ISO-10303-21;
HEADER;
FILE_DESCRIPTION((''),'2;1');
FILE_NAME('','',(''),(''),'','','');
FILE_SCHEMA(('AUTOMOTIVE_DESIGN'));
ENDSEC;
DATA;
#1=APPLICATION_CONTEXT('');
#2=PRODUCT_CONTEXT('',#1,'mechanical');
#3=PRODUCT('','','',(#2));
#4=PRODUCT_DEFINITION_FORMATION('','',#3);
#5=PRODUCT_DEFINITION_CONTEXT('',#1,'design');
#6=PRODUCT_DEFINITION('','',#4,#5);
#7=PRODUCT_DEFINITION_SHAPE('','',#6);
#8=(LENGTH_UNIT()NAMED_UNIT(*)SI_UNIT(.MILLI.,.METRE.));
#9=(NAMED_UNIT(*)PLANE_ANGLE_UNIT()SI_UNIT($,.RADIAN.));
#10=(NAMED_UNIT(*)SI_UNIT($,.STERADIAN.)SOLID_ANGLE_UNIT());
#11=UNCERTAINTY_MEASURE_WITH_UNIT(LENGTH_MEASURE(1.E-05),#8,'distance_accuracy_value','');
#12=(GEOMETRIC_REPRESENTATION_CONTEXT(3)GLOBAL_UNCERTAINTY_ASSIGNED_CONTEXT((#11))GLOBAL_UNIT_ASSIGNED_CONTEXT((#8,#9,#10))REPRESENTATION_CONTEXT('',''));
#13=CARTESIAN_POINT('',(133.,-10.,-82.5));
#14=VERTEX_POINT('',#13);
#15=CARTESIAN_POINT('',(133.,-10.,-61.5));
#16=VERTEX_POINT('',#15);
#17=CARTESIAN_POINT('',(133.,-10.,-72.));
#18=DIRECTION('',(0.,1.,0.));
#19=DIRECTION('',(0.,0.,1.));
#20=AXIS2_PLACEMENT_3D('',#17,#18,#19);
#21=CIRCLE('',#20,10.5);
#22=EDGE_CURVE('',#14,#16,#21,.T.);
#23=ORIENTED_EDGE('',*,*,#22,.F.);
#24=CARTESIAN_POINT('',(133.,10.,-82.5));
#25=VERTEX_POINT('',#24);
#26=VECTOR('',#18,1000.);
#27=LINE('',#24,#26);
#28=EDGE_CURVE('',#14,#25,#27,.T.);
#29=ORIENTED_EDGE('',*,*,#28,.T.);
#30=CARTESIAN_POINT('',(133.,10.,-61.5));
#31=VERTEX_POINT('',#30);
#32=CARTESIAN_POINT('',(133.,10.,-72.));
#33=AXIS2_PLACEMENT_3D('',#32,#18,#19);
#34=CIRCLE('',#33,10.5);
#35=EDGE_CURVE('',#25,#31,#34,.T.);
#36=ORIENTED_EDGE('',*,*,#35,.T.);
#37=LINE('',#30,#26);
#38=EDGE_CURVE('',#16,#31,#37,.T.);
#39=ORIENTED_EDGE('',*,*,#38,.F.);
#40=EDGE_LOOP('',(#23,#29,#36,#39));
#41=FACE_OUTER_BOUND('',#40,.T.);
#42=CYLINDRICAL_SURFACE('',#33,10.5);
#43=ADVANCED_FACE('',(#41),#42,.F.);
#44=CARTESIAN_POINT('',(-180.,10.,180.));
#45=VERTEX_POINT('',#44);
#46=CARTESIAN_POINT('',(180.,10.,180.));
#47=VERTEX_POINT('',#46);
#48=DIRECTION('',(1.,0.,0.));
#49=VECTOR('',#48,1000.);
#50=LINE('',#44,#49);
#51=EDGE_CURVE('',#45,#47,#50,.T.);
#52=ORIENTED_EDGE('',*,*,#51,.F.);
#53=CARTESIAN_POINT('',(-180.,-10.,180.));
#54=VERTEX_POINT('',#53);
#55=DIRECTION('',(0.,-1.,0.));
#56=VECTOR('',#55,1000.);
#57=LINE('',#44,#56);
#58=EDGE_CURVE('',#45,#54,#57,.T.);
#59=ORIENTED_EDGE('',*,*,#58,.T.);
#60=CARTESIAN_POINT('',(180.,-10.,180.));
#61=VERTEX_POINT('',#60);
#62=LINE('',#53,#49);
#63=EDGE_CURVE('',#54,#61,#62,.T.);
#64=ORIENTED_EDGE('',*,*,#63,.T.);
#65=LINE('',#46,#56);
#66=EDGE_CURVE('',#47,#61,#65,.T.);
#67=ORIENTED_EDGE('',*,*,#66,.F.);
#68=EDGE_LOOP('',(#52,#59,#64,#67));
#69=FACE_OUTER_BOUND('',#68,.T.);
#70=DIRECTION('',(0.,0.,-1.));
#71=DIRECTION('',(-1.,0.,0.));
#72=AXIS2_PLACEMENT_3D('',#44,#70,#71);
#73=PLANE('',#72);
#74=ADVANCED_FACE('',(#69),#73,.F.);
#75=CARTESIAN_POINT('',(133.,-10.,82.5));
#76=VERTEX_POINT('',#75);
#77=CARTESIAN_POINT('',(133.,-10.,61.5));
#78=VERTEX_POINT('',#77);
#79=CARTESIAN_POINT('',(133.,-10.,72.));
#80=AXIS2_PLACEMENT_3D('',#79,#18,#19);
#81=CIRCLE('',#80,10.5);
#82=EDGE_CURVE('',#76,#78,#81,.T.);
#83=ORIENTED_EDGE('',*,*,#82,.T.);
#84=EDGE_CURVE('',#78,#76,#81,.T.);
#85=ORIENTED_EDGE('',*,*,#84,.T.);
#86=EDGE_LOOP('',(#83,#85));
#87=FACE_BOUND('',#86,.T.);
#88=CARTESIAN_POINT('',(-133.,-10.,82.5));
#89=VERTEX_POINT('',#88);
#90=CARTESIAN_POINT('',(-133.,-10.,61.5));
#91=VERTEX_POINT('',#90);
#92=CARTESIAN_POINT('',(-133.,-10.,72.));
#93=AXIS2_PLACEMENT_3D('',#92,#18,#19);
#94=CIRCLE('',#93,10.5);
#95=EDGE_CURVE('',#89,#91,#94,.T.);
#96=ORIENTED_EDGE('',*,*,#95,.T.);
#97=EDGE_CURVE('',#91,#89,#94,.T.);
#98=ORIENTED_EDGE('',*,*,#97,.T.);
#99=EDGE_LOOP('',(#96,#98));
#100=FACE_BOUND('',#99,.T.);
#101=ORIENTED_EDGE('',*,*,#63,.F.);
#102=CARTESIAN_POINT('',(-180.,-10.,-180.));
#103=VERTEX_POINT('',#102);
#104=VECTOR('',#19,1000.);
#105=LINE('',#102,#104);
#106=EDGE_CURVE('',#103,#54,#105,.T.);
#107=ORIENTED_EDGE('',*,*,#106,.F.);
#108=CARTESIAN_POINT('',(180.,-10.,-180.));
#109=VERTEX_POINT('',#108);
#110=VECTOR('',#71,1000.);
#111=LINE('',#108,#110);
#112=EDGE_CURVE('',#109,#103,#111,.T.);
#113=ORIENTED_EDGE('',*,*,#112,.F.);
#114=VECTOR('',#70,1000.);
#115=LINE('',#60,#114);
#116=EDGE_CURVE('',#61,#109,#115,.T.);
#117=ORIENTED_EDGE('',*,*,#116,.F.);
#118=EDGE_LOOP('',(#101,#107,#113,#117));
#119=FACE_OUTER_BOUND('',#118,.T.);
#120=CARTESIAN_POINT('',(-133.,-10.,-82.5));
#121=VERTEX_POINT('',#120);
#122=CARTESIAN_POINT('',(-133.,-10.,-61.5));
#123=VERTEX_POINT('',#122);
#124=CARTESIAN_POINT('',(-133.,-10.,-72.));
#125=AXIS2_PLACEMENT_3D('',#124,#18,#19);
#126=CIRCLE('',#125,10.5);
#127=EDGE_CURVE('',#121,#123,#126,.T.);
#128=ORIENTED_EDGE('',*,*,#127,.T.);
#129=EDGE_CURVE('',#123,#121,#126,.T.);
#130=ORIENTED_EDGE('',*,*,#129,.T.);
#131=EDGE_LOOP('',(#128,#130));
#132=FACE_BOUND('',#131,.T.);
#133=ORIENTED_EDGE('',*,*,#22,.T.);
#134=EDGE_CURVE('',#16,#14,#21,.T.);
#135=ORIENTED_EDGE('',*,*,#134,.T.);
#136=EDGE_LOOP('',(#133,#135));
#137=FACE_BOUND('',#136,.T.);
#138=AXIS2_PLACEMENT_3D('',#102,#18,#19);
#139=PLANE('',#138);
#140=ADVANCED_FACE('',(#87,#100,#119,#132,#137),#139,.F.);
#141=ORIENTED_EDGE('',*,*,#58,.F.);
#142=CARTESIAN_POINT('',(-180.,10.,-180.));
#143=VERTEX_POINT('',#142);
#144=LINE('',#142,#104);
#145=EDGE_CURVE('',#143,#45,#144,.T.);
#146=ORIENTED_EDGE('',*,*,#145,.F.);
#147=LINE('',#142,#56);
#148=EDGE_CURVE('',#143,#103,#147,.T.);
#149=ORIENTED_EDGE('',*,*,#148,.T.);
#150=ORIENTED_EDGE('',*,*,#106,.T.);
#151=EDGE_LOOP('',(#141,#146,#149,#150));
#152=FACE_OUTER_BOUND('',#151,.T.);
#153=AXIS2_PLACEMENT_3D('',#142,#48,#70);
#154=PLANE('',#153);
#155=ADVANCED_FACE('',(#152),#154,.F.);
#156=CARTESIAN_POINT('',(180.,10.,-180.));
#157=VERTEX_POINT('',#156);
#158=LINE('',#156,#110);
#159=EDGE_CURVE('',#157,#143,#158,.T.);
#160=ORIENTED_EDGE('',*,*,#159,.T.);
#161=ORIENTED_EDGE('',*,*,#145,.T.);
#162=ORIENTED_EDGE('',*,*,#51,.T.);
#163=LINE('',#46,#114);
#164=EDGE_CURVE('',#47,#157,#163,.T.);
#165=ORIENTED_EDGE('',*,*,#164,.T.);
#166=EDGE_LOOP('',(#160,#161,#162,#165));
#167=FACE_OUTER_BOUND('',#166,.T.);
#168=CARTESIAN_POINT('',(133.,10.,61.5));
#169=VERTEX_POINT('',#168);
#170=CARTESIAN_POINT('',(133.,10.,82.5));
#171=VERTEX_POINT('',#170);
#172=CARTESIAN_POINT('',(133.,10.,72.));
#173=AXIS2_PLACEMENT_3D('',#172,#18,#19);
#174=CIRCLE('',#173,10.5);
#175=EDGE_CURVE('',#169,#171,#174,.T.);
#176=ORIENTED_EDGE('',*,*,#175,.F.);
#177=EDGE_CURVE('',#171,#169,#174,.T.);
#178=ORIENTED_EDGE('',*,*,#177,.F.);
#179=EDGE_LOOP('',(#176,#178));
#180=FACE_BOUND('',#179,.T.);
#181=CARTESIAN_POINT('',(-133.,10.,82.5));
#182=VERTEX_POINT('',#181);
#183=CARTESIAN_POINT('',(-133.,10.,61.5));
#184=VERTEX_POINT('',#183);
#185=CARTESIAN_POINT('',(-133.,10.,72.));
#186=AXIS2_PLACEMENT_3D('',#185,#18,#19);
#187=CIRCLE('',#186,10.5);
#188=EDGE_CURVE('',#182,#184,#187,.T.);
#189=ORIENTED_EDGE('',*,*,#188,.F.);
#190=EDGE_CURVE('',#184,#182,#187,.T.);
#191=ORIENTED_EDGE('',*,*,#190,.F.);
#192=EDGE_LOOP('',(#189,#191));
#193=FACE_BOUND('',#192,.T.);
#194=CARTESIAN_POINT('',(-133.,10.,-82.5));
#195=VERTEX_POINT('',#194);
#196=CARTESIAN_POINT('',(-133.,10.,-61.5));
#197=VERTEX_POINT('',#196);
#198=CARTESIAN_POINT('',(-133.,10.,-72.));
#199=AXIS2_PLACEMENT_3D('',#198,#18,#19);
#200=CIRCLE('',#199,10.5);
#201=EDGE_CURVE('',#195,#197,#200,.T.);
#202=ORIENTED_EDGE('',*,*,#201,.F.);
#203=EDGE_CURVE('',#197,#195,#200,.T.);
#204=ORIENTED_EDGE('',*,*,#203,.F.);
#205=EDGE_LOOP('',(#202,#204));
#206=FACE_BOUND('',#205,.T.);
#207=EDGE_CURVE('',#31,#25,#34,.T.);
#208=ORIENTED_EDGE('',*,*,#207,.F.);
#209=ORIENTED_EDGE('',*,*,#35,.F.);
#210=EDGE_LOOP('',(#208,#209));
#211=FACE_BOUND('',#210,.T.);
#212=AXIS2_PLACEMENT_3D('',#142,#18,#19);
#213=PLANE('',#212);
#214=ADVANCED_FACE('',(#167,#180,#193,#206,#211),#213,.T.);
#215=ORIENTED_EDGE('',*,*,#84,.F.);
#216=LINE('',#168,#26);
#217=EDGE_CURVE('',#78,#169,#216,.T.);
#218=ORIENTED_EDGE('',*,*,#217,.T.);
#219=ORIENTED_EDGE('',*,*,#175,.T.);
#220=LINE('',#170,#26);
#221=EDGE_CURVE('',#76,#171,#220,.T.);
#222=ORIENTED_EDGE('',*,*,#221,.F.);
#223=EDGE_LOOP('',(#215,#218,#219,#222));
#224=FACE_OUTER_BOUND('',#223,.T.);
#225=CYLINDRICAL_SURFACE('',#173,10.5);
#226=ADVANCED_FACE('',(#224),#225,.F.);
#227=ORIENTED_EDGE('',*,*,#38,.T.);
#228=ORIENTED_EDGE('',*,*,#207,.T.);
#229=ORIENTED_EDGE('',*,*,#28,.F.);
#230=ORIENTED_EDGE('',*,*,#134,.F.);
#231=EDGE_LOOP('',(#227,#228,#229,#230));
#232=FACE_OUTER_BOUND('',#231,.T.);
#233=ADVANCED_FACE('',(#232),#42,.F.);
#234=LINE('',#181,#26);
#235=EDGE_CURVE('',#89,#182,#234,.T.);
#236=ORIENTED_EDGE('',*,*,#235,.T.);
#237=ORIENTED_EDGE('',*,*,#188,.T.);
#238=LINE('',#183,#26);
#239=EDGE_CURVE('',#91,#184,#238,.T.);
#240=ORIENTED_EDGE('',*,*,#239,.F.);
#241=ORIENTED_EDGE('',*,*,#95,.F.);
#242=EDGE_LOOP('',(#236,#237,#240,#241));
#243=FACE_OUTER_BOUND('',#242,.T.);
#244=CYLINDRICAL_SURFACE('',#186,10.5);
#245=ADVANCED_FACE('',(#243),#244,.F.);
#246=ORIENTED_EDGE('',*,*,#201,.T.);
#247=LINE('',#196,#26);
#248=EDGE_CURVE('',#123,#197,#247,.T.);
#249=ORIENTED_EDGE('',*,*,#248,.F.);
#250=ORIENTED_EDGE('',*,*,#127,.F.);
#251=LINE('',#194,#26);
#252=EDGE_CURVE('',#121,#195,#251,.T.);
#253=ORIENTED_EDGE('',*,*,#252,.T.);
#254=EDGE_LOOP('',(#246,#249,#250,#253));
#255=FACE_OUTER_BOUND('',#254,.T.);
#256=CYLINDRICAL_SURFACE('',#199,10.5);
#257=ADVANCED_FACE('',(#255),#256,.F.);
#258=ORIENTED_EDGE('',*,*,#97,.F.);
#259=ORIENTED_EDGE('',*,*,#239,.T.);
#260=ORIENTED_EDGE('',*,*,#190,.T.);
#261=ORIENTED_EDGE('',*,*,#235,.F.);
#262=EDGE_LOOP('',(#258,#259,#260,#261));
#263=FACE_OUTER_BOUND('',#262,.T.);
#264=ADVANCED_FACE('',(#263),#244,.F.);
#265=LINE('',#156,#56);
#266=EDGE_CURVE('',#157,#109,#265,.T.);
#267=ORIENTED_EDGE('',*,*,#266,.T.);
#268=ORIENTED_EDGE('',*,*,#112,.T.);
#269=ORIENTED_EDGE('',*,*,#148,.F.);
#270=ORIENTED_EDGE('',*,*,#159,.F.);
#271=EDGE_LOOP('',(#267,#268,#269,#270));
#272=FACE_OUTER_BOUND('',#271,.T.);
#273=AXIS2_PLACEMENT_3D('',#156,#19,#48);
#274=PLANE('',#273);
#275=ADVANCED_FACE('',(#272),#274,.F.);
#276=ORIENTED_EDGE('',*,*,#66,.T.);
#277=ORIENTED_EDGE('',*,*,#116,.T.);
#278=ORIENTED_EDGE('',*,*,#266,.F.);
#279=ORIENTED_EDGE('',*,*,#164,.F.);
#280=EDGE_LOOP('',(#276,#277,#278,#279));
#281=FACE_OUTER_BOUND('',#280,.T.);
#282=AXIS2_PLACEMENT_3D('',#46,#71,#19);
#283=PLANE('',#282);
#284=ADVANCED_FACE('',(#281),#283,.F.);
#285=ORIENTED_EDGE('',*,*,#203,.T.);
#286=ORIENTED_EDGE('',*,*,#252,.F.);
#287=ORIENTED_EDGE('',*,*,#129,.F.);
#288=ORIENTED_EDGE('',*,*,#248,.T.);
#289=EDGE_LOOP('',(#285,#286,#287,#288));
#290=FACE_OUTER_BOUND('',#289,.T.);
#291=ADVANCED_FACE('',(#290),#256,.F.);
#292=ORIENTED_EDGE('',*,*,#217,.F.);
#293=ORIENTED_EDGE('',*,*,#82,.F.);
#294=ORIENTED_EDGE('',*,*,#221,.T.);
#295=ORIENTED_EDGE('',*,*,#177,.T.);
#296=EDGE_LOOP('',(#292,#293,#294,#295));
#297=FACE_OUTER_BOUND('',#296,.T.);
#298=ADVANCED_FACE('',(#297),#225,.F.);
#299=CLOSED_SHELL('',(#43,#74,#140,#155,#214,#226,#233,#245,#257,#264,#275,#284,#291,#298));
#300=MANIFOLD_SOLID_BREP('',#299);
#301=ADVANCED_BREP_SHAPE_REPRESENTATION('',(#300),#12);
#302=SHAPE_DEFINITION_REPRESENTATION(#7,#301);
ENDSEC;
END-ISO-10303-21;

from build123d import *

# Parameters (mm, degrees)
SKETCH1_W            = 360
SKETCH1_H            = 360
EXTRUDE1_DEPTH       = 10
M24_TAPPED_HOLE1_D   = 21
LPATTERN2_COUNT      = 2
LPATTERN2_PITCH      = 144
LPATTERN2_COUNT_DIR2 = 2
LPATTERN2_PITCH_DIR2 = 266


with BuildPart() as part:
    # Sketch1 → Extrude1 (new, symmetric)
    with BuildSketch(Plane(origin=(0, 0, 0), x_dir=(1, 0, 0), z_dir=(0, 1, 0))):
        Rectangle(SKETCH1_W, SKETCH1_H)
    extrude(amount=EXTRUDE1_DEPTH, both=True)

    # M24 Tapped Hole1 (through all)
    with Locations(Plane(origin=(0, 10, 0), x_dir=(-1, 0, 0), z_dir=(0, 1, 0))):
        with Locations((133, -72)):
            m24_tapped_hole1 = Hole(M24_TAPPED_HOLE1_D / 2)

    # LPattern2: M24 Tapped Hole1 2 × 2
    with Locations(*[(j * LPATTERN2_PITCH_DIR2, 0, i * LPATTERN2_PITCH) for i in range(LPATTERN2_COUNT) for j in range(LPATTERN2_COUNT_DIR2) if (i, j) != (0, 0)]):
        add(m24_tapped_hole1, mode=Mode.SUBTRACT)


solid = part.part
